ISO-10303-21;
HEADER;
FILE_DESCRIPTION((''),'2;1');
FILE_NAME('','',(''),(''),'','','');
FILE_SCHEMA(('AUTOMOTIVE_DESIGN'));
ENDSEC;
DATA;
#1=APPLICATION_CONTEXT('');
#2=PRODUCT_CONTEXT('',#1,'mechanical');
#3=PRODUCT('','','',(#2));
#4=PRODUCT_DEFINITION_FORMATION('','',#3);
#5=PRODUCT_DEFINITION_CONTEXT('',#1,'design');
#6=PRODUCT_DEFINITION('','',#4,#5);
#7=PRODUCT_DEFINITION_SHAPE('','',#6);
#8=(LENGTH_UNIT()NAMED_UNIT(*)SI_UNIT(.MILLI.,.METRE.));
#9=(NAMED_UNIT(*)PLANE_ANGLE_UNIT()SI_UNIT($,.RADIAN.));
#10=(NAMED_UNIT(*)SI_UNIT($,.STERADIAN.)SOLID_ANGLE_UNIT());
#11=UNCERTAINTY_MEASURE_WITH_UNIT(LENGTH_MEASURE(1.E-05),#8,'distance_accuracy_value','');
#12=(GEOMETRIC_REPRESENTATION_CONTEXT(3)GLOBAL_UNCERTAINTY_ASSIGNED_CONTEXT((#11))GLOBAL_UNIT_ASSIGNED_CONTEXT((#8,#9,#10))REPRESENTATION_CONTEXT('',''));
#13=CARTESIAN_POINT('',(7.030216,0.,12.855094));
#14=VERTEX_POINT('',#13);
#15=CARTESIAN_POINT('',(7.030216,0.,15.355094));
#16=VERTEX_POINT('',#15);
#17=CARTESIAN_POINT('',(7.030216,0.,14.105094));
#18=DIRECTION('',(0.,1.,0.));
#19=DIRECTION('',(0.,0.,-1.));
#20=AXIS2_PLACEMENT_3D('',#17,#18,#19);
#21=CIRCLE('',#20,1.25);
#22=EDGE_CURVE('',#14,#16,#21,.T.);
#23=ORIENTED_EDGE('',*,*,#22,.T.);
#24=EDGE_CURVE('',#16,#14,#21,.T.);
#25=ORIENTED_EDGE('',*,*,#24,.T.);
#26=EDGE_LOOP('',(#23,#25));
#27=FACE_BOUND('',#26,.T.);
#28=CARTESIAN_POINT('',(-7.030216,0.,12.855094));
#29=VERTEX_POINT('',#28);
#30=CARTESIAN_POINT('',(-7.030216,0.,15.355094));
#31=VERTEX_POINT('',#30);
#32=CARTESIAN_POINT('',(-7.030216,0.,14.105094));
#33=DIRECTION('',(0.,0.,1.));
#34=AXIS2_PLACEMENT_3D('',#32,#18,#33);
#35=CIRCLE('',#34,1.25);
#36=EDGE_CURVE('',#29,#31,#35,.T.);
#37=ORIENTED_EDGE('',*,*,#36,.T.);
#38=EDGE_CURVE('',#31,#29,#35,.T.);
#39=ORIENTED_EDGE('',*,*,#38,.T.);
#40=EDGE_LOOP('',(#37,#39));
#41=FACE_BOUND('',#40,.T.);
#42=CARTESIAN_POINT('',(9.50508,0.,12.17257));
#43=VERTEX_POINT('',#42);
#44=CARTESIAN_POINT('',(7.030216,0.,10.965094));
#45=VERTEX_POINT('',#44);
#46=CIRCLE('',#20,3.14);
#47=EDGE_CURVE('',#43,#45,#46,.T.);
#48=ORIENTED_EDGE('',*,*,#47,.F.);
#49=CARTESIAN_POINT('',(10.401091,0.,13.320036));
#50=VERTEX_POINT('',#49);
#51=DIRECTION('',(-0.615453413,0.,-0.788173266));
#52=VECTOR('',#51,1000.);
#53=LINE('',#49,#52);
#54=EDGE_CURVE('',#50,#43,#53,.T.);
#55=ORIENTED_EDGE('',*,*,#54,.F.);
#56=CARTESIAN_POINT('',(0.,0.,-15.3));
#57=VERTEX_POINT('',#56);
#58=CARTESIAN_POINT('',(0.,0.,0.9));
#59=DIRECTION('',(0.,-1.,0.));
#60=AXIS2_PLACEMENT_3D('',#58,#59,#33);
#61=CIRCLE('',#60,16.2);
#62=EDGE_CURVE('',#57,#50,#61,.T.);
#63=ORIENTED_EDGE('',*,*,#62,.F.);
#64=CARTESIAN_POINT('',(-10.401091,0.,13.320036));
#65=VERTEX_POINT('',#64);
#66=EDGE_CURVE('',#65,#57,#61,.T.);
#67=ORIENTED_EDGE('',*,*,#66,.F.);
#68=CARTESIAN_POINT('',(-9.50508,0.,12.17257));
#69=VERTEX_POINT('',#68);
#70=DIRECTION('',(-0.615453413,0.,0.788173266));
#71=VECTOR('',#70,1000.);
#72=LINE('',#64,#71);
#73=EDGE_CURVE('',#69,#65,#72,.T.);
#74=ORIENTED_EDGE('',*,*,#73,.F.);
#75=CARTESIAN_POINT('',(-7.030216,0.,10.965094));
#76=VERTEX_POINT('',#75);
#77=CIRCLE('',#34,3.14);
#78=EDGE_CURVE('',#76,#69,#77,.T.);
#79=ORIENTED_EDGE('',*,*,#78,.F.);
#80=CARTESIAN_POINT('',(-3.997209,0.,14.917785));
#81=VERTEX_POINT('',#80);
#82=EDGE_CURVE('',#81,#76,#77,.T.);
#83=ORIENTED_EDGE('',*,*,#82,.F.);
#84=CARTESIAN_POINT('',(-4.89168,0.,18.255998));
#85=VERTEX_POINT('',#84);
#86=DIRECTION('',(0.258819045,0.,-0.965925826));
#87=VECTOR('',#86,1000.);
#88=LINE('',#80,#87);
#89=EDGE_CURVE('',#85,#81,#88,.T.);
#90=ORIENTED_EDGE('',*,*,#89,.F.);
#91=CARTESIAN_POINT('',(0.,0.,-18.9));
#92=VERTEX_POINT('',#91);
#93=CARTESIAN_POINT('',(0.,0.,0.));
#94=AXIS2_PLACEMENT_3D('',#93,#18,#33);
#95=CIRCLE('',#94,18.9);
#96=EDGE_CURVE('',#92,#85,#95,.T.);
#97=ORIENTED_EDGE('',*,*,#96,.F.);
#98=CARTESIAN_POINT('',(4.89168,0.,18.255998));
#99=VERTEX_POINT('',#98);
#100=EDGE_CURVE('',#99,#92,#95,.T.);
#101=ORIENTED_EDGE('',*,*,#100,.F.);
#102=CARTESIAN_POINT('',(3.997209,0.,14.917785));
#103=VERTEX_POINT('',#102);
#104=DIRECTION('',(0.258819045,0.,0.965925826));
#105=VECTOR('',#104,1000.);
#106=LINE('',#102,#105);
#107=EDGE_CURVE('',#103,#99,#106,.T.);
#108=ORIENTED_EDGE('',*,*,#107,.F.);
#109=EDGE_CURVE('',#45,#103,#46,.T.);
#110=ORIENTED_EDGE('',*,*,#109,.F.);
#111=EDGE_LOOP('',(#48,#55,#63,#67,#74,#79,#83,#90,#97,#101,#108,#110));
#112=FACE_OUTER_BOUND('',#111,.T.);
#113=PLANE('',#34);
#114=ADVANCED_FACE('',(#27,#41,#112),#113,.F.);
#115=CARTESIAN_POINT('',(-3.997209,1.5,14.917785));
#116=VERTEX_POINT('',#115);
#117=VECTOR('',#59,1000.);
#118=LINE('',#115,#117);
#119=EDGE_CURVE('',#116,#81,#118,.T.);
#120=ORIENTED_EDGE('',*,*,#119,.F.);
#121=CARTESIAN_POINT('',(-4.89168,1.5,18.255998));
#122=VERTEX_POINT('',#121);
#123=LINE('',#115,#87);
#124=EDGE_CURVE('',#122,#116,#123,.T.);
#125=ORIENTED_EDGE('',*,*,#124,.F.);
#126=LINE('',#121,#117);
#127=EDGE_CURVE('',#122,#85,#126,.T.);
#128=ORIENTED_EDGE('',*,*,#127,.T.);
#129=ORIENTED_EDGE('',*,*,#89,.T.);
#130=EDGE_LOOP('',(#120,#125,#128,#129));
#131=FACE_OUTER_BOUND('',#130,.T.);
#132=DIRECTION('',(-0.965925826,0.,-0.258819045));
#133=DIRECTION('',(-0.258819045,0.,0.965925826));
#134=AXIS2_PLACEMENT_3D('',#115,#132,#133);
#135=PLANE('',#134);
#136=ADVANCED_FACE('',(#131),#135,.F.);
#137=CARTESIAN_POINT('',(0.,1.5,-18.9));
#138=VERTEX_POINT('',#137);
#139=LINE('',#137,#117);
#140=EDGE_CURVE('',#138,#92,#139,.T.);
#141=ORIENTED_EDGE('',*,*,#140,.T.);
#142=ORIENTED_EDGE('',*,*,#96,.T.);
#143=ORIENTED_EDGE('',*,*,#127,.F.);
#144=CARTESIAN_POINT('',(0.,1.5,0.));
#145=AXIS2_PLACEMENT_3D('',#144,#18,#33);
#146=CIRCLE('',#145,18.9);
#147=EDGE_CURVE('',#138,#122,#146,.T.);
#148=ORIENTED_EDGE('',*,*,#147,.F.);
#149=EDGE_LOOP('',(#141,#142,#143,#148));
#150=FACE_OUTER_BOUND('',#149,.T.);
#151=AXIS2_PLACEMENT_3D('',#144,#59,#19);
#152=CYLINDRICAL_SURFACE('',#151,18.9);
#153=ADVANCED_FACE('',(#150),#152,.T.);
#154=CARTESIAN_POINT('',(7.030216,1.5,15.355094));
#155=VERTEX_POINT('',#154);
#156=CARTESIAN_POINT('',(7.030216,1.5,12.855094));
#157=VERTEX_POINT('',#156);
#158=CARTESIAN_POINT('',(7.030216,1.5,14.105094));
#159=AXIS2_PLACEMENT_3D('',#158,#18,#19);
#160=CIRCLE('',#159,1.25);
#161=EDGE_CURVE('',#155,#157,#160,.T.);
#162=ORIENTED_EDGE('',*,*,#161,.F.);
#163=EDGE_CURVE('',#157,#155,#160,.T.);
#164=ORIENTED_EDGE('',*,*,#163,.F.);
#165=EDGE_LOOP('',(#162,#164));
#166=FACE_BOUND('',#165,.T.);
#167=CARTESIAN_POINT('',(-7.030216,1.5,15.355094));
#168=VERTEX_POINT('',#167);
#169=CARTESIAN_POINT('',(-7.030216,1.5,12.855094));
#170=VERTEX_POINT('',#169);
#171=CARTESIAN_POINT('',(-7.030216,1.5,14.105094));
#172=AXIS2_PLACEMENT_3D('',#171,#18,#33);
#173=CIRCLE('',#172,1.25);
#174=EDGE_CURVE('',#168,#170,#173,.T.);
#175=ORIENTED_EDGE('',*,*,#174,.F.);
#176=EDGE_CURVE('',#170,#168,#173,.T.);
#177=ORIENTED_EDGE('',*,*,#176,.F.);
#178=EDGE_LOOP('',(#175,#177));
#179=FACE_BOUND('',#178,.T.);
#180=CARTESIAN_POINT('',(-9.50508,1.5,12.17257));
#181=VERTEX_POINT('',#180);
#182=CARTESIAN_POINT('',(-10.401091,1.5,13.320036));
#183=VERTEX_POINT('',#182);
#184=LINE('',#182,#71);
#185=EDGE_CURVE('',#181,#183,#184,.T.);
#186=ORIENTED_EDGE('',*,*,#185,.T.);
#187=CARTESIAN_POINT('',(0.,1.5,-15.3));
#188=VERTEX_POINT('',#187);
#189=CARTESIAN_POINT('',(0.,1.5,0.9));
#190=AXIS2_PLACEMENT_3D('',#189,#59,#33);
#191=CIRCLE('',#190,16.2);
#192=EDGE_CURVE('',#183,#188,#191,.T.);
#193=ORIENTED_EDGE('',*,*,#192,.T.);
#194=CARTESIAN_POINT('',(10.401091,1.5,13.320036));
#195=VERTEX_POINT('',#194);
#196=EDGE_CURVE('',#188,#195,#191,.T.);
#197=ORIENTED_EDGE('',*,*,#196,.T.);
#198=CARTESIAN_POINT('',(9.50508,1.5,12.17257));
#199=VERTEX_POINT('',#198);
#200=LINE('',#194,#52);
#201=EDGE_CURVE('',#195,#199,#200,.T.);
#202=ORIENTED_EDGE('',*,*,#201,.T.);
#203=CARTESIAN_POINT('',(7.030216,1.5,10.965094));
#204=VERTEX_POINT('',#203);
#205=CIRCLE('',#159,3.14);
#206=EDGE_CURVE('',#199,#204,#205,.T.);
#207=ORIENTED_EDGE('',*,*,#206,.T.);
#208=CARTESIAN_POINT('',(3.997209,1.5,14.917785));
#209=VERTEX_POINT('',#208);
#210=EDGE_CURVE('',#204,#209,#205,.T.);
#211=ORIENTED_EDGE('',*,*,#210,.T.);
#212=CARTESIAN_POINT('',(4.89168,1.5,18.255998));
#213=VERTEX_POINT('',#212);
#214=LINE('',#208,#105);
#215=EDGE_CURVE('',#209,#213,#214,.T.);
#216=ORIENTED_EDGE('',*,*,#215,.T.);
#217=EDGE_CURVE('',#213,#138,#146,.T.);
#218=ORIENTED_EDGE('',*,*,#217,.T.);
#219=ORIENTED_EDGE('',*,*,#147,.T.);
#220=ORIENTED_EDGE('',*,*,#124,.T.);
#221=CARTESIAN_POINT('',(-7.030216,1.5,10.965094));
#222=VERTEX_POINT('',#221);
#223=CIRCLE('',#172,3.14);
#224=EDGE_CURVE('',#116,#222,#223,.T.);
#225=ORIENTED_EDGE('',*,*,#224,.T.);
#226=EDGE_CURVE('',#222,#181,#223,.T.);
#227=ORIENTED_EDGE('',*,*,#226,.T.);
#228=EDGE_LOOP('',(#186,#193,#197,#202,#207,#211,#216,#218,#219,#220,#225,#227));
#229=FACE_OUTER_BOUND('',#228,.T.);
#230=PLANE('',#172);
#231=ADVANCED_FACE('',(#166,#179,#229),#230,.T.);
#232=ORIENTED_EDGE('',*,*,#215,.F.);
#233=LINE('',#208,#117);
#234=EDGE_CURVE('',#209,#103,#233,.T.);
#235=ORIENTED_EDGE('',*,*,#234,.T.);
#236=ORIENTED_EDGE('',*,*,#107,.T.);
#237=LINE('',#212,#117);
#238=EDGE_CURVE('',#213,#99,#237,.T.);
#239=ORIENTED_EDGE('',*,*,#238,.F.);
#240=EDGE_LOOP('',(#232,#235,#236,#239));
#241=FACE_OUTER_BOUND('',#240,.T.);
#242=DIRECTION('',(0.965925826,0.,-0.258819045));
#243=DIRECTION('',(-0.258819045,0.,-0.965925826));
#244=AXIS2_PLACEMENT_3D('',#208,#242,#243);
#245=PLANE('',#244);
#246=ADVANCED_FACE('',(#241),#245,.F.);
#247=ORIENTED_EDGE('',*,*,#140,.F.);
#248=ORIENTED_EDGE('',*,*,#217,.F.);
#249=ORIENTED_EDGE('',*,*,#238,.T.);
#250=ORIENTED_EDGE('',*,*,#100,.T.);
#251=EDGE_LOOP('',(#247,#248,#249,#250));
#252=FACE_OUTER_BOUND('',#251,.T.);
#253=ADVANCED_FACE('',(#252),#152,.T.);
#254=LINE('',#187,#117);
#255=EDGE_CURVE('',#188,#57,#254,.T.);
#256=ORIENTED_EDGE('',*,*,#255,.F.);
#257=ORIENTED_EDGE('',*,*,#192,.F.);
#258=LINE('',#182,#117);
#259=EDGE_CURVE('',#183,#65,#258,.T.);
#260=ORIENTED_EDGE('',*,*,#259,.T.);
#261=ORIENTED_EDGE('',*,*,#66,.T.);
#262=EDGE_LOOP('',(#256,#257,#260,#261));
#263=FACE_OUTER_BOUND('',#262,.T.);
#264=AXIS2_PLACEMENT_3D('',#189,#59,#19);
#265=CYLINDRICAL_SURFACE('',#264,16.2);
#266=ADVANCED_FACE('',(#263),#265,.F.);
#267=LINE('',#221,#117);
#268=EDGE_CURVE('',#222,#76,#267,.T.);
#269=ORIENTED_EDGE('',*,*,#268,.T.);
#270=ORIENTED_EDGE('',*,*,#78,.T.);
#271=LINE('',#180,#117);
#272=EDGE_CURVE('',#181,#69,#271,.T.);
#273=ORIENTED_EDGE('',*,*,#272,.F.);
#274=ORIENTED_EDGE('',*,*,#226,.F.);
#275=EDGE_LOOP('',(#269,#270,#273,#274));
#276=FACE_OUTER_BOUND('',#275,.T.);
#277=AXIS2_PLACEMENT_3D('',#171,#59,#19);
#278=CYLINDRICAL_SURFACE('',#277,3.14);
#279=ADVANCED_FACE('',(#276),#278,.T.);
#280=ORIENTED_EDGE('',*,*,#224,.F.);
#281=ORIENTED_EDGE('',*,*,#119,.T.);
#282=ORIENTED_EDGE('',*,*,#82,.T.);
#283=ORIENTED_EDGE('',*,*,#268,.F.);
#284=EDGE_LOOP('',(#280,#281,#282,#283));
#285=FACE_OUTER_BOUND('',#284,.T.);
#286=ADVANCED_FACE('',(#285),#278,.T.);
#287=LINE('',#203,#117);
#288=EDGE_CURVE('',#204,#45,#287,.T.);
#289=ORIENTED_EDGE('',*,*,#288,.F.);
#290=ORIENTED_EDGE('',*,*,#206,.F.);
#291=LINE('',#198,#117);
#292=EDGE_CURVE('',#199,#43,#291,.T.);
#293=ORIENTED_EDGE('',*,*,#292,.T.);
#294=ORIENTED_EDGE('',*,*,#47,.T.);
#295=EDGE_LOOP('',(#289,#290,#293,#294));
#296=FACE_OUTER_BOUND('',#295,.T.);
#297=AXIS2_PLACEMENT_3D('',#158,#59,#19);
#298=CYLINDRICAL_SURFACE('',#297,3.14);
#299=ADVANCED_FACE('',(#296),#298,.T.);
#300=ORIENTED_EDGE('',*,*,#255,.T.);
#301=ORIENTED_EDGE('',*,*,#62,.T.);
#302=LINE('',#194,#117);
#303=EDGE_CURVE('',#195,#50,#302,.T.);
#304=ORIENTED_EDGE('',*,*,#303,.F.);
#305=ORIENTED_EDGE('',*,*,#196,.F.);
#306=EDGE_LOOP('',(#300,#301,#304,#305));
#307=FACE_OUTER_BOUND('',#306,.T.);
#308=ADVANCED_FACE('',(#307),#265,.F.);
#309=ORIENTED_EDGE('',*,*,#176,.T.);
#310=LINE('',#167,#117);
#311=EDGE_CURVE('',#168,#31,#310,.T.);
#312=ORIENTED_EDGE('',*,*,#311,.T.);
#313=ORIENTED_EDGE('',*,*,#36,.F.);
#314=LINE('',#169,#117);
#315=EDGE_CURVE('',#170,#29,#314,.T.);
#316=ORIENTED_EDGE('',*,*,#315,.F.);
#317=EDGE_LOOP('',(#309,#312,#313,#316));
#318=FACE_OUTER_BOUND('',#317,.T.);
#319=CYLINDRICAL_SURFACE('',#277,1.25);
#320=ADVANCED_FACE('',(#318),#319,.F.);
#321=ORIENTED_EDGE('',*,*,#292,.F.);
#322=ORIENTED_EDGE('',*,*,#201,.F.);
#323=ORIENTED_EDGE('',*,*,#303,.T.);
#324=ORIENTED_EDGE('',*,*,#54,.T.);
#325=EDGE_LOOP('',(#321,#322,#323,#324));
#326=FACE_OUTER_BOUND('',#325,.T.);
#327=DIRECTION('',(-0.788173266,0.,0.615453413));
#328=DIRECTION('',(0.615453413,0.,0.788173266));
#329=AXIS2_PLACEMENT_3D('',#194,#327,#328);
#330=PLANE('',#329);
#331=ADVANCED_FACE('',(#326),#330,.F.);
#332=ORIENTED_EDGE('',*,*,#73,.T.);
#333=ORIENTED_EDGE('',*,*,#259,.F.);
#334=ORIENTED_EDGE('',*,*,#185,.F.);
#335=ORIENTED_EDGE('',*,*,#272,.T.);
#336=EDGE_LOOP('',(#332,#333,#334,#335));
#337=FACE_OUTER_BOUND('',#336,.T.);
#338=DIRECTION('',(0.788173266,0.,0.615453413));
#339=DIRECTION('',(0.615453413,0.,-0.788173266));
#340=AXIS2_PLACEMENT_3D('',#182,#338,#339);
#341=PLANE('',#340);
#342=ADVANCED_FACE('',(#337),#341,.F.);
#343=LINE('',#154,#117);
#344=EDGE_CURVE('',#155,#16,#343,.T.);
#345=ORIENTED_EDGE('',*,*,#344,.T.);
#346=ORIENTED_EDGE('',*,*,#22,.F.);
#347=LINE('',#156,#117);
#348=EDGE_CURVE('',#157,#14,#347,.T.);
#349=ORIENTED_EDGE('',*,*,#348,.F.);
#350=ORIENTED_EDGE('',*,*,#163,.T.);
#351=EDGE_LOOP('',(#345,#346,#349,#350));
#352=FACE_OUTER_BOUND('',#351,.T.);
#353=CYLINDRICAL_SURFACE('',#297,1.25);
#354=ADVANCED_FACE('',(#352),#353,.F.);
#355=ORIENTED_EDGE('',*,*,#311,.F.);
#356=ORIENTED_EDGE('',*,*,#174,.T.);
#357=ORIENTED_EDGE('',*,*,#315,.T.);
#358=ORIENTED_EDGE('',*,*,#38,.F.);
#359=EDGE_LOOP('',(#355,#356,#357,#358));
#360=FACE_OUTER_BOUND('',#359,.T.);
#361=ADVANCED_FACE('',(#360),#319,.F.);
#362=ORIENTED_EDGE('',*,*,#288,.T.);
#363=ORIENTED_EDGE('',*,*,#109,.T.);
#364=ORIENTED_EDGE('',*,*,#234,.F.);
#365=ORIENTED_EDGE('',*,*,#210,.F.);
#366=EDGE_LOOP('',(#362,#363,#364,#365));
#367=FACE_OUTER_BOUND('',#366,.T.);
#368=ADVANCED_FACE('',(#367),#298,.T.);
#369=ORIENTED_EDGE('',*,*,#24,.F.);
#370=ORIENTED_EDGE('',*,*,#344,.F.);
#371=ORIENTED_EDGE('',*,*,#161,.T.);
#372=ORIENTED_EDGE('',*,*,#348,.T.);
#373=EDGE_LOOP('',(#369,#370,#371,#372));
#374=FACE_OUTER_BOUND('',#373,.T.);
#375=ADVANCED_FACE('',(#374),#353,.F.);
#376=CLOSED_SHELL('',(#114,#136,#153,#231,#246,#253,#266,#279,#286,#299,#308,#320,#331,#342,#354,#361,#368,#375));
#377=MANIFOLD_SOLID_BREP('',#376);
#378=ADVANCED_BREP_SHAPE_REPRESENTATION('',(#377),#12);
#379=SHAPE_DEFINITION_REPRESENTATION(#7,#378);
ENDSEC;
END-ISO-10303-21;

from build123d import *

# Parameters (mm, degrees)
SKETCH2_R           = 1.25
BOSS_EXTRUDE1_DEPTH = 1.5


with BuildPart() as part:
    # Sketch2 → Boss-Extrude1 (new body)
    with BuildSketch(Plane(origin=(0, 0, 0), x_dir=(1, 0, 0), z_dir=(0, 1, 0))):
        with BuildLine():
            Line((-10.401091034, -13.320036445), (-9.505079721, -12.172569963))
            ThreePointArc((-9.505079721, -12.172569963), (-5.62952549, -11.294814862), (-3.997208572, -14.91778548))
            Line((-3.997208572, -14.91778548), (-4.891679952, -18.255998117))
            ThreePointArc((-4.891679952, -18.255998117), (0, 18.9), (4.891679952, -18.255998117))
            Line((4.891679952, -18.255998117), (3.997208572, -14.91778548))
            ThreePointArc((3.997208572, -14.91778548), (5.62952549, -11.294814862), (9.505079721, -12.172569963))
            Line((9.505079721, -12.172569963), (10.401091034, -13.320036445))
            ThreePointArc((10.401091034, -13.320036445), (0, 15.3), (-10.401091034, -13.320036445))
        make_face()
        with Locations(Location((-7.030215667, -14.105093678, 0), (0, 0, 270))):
            Circle(SKETCH2_R, mode=Mode.SUBTRACT)
        with Locations(Location((7.030215667, -14.105093678, 0), (0, 0, 90))):
            Circle(SKETCH2_R, mode=Mode.SUBTRACT)
    extrude(amount=BOSS_EXTRUDE1_DEPTH)


solid = part.part
